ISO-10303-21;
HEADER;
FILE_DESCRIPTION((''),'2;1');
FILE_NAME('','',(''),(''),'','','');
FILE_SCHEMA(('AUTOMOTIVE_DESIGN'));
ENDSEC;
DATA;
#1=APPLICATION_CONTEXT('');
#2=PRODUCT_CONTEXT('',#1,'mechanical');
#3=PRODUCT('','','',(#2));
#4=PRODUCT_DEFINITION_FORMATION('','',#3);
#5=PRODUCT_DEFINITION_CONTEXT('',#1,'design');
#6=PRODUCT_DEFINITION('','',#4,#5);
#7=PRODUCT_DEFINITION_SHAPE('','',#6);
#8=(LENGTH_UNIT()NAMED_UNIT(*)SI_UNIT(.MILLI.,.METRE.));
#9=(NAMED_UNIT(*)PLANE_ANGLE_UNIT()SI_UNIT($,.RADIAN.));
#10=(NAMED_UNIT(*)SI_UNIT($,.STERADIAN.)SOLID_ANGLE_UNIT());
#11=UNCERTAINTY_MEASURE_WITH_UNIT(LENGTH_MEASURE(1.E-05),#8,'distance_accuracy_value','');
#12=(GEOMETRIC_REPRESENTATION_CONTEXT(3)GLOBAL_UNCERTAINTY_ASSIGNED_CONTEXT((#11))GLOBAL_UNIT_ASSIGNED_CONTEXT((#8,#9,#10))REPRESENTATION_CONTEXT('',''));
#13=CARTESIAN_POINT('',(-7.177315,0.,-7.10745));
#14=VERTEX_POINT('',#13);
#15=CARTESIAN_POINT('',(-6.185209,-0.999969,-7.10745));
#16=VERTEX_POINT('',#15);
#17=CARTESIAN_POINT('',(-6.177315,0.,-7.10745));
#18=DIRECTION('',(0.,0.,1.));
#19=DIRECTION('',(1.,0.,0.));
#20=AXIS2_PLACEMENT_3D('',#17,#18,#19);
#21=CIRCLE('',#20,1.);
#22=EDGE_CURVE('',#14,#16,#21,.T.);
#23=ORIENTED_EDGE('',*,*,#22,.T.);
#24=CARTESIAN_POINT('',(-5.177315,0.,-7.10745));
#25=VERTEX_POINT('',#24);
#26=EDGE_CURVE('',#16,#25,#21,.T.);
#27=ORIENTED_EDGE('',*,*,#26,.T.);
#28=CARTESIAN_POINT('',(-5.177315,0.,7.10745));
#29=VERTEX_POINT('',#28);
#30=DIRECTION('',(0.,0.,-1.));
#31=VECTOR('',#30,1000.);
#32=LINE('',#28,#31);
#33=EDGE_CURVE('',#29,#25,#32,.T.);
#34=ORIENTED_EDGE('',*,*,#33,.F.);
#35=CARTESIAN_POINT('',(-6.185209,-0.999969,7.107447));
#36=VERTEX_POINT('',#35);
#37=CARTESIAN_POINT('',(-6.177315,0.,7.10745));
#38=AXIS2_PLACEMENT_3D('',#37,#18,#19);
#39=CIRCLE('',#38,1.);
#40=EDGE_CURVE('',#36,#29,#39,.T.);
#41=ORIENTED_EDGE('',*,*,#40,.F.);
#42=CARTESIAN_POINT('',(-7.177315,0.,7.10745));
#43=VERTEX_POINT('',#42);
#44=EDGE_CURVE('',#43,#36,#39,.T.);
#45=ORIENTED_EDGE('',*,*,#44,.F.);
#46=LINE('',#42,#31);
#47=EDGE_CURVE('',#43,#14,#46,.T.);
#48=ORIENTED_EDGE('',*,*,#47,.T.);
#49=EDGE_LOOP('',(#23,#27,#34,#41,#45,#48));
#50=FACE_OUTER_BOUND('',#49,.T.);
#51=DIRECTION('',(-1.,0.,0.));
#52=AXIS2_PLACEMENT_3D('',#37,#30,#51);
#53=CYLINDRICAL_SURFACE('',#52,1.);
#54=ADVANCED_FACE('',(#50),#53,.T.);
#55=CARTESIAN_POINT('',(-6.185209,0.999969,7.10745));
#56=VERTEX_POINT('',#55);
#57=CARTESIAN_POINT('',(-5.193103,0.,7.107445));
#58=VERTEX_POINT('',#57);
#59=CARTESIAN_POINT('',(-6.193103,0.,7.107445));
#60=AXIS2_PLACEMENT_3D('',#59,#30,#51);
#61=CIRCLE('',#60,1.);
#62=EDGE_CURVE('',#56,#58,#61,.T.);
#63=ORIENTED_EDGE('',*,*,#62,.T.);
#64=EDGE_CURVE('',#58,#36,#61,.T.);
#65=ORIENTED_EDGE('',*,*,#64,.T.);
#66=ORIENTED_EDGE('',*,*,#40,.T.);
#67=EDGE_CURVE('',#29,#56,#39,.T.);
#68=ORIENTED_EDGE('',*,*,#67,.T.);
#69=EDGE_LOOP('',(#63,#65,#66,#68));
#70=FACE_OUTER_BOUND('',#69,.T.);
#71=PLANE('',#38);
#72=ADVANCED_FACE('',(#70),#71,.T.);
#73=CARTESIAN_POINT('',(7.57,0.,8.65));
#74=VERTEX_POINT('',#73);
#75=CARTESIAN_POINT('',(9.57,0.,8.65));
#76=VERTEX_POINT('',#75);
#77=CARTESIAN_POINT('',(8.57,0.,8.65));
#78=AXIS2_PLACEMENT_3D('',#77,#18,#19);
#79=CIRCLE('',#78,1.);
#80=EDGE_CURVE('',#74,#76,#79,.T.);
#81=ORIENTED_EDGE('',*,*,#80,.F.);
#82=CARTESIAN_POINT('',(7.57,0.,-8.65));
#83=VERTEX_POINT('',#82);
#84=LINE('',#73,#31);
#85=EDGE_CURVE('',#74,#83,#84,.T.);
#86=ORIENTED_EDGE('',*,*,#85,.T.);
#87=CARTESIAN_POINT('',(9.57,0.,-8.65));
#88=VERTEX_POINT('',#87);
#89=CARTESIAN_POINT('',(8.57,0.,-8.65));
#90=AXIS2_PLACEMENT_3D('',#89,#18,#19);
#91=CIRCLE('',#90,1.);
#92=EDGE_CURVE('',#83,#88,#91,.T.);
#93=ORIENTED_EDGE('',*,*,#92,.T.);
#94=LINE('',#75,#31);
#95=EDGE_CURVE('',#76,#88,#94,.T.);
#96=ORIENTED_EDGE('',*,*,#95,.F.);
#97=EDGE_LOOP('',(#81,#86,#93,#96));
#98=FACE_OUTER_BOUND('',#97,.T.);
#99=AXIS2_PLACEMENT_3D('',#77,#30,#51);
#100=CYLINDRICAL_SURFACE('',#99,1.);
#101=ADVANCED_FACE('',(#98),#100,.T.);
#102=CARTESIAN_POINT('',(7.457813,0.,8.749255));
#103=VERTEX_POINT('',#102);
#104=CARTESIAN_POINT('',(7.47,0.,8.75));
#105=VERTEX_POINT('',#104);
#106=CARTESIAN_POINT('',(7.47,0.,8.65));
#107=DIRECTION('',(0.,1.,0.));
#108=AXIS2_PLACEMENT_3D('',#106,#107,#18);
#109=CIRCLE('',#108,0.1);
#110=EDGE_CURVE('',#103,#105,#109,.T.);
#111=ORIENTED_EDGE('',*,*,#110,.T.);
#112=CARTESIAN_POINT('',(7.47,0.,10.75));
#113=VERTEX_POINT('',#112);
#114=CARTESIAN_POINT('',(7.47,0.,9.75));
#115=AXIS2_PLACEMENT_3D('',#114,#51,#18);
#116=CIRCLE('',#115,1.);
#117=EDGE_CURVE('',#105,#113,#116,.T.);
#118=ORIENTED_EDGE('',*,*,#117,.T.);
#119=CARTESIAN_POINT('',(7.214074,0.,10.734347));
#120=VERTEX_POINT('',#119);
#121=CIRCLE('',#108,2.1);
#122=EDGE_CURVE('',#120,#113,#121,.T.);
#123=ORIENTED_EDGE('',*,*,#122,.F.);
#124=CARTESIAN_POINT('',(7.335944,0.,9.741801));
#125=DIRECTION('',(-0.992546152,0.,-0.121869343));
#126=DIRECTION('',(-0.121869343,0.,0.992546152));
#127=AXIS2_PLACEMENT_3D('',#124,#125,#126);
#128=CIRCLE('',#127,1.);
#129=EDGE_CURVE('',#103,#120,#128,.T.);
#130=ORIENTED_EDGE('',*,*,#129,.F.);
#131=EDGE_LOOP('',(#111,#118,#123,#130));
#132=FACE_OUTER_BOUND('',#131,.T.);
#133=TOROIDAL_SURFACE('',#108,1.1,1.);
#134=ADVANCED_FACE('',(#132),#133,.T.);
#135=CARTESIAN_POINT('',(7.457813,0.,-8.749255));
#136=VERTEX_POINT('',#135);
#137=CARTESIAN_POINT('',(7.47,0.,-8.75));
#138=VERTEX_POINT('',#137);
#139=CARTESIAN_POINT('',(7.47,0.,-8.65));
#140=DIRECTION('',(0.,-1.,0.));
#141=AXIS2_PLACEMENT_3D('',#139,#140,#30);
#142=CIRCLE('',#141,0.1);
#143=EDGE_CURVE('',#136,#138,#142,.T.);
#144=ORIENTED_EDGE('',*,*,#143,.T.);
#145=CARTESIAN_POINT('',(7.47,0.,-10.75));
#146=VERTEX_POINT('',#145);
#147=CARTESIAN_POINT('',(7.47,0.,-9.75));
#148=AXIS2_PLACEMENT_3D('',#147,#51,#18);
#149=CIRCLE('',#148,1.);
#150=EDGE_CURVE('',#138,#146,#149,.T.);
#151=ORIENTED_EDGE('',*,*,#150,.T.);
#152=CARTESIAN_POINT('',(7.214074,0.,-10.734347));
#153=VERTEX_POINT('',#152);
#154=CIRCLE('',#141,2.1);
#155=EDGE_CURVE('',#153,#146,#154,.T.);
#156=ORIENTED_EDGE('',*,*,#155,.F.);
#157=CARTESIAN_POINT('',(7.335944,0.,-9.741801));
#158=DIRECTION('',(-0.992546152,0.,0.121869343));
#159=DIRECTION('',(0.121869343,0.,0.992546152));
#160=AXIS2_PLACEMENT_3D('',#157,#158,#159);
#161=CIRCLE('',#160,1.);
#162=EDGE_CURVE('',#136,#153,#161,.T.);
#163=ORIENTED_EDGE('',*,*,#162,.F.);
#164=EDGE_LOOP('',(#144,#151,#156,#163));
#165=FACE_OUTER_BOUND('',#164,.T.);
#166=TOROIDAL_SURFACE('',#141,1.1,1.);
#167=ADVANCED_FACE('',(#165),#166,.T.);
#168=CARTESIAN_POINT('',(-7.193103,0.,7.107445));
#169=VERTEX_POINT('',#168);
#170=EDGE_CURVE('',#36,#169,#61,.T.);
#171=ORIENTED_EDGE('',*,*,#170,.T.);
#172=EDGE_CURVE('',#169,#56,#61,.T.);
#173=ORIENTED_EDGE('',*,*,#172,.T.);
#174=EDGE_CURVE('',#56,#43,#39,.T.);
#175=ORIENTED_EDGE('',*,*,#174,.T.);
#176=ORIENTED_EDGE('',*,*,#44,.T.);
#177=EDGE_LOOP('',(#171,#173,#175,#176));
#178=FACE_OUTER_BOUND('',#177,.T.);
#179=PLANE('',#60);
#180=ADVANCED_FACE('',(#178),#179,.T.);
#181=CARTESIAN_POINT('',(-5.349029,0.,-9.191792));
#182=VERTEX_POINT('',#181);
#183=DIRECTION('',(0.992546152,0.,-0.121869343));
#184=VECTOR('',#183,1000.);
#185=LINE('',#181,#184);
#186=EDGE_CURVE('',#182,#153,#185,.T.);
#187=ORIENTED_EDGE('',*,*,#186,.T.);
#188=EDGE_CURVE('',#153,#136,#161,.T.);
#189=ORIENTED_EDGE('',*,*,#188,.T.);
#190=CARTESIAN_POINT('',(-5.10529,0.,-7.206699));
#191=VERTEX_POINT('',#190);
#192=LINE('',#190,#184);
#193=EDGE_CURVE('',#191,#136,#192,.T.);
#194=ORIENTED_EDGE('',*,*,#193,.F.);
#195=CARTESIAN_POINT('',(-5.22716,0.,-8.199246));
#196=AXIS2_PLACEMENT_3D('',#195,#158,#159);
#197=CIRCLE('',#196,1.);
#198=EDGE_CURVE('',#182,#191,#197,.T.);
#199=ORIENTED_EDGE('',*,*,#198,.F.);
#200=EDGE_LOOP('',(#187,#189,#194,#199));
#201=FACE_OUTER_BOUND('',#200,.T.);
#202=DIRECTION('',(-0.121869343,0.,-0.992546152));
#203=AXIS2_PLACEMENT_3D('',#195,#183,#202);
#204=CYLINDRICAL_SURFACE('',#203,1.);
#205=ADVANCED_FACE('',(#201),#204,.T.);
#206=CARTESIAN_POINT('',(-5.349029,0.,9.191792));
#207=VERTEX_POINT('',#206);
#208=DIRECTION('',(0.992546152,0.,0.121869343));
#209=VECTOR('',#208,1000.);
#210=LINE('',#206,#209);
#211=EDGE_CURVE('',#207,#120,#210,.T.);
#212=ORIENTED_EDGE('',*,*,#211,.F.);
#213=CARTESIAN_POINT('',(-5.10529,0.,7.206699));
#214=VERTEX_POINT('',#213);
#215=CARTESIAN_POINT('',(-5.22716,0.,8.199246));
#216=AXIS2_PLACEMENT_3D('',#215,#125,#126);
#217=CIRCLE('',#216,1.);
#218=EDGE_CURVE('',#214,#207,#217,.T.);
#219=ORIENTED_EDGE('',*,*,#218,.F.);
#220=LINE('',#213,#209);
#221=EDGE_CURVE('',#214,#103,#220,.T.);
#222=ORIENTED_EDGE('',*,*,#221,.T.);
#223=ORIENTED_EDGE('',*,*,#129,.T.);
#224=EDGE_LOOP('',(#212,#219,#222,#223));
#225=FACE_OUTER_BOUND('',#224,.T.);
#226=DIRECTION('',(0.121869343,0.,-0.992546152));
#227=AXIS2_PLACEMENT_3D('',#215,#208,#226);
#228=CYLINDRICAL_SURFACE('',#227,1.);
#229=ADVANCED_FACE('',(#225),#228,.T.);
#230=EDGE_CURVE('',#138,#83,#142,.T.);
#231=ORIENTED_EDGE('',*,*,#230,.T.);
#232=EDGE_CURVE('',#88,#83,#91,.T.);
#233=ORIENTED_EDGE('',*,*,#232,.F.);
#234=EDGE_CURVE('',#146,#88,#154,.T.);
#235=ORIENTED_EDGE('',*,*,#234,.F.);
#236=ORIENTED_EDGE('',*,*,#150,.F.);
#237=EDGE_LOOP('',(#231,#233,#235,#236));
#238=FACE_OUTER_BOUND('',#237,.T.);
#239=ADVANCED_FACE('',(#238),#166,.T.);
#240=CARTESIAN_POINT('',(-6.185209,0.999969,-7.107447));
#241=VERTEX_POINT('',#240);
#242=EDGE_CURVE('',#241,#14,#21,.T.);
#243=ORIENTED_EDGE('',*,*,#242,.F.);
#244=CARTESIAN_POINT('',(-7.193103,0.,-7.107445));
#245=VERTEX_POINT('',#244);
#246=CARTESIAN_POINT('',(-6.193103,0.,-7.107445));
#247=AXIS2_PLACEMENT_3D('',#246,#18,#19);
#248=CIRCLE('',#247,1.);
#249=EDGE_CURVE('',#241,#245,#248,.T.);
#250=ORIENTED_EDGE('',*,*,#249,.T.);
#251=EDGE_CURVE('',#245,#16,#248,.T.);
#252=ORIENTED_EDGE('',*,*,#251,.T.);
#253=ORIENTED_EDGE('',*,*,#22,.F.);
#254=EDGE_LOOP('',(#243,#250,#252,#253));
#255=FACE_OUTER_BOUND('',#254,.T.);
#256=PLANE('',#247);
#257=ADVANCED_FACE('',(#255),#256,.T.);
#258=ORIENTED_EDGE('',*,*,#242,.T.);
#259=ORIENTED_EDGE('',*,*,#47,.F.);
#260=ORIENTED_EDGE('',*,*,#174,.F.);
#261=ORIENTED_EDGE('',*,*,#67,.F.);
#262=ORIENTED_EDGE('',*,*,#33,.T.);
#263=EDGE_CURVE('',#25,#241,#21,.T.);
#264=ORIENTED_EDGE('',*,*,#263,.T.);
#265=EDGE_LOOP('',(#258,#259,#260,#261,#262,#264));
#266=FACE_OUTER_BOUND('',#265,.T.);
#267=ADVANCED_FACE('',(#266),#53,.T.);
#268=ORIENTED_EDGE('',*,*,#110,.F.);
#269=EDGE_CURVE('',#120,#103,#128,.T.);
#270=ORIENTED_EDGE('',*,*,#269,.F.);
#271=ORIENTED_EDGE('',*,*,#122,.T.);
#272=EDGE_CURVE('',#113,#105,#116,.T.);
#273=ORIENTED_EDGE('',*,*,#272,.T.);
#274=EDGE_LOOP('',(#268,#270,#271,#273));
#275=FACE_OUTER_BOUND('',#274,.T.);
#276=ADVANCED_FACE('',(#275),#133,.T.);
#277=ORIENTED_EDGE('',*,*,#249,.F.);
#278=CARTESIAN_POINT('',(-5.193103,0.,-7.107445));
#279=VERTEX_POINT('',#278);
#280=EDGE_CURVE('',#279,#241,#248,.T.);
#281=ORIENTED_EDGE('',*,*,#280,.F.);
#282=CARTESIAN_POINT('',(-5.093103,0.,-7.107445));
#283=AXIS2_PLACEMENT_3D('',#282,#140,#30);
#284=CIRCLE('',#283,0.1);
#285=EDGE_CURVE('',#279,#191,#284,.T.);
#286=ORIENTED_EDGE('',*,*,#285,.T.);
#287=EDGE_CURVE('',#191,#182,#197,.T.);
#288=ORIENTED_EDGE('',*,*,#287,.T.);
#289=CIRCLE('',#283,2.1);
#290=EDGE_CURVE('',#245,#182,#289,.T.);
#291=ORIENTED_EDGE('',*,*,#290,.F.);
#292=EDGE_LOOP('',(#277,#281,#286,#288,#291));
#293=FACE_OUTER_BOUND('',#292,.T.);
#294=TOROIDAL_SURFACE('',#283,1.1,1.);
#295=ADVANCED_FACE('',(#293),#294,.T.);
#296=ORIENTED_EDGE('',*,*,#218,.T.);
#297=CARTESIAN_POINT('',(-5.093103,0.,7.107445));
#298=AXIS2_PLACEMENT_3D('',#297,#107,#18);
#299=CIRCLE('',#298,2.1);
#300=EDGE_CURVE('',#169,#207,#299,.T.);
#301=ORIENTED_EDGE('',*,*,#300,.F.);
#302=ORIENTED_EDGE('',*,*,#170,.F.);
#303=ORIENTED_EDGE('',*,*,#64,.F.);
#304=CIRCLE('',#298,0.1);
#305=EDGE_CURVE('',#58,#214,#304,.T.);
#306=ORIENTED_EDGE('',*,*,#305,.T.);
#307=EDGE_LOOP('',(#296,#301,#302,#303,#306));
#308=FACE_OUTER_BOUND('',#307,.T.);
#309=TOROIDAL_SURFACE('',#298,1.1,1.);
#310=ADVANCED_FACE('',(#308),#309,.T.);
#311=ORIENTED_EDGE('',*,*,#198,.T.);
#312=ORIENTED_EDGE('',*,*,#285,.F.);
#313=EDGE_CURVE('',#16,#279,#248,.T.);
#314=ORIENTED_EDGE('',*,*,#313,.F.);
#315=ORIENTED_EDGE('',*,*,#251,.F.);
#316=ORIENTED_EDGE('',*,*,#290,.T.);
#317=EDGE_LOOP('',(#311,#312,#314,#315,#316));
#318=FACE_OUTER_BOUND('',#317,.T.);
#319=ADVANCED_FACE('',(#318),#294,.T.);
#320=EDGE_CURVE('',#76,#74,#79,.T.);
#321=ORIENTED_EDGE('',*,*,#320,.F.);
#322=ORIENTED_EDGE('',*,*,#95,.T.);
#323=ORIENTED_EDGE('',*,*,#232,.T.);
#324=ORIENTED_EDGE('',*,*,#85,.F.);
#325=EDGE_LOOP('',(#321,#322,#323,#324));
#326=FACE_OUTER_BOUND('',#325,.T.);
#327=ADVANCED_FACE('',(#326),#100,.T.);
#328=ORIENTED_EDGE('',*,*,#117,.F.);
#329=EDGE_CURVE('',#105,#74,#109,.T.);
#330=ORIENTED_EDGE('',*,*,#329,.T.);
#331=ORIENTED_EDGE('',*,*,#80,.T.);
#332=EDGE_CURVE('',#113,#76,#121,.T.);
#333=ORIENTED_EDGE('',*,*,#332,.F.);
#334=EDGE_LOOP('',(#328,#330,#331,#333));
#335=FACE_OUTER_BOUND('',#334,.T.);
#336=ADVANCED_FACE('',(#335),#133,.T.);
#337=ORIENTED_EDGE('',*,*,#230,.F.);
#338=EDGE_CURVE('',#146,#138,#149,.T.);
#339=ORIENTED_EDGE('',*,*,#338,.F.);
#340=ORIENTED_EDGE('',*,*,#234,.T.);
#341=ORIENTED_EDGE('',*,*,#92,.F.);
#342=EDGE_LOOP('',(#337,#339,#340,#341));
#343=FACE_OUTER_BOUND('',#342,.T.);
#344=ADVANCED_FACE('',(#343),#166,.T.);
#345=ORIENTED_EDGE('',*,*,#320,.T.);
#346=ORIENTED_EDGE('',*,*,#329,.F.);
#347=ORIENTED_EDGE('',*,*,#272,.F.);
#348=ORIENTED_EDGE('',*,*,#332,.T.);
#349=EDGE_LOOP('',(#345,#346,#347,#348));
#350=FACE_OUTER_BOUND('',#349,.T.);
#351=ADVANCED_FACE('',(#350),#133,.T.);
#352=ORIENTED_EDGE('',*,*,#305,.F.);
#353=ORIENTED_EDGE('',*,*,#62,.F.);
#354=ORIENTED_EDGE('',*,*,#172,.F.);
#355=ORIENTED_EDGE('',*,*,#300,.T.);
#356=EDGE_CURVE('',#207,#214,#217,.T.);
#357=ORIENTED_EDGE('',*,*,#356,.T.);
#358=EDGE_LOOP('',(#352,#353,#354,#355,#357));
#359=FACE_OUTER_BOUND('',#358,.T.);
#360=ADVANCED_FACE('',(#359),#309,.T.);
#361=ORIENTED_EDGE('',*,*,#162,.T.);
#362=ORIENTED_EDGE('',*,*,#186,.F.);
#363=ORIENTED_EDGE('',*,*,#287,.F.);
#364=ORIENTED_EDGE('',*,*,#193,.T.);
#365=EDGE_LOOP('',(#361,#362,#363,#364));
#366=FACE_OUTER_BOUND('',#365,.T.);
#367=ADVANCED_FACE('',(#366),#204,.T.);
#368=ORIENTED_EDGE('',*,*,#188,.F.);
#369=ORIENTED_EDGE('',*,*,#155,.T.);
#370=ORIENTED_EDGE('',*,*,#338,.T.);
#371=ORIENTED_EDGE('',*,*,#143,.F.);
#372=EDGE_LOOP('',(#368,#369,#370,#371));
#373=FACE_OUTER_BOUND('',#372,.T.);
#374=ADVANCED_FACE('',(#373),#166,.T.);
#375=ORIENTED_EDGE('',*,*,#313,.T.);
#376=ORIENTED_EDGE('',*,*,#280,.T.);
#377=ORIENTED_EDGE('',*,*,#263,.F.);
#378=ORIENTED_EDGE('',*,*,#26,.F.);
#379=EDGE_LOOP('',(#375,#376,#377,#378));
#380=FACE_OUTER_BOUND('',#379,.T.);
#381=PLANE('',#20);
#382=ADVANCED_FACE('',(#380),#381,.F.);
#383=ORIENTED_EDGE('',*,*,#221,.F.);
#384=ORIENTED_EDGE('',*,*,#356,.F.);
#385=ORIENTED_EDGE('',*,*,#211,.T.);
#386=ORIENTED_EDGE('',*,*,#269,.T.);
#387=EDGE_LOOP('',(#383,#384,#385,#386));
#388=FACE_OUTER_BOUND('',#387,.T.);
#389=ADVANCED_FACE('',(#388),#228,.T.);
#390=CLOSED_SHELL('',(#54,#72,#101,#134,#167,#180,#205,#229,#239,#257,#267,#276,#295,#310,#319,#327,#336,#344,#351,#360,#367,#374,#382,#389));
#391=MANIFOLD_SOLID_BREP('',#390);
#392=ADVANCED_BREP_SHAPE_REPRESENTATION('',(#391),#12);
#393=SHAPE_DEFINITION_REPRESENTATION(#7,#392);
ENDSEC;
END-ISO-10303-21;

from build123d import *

# Parameters (mm, degrees)
EXTRUDE_1_DEPTH      = 8.65
EXTRUDE_1_DEPTH_BACK = 8.65
SKETCH_1_R           = 1
SKETCH_2_R           = 1
REVOLVE_1_ANGLE      = 97
SKETCH_3_R           = 1
REVOLVE_2_ANGLE      = 97
SKETCH_4_R           = 1
EXTRUDE_2_DEPTH      = 12.65745
SKETCH_5_R           = 1
EXTRUDE_3_DEPTH      = 12.65745
SKETCH_6_R           = 1
REVOLVE_3_ANGLE      = 83
SKETCH_7_R           = 1
REVOLVE_4_ANGLE      = 83
EXTRUDE_4_DEPTH      = 7.10745
EXTRUDE_4_DEPTH_BACK = 7.10745
SKETCH_8_R           = 1


with BuildPart() as part:
    # 草图1 → 凸台-拉伸1 (new, two sides: drawn at the far end of the back side and taken through both)
    with BuildSketch(Plane.XY.offset(-EXTRUDE_1_DEPTH_BACK)):
        with Locations((8.57, 0)):
            Circle(SKETCH_1_R)
    extrude(amount=EXTRUDE_1_DEPTH + EXTRUDE_1_DEPTH_BACK)

    # 草图2 → 旋转1 (revolve)
    with BuildSketch(Plane(origin=(0, 0, -8.65), x_dir=(-1, 0, 0), z_dir=(0, 0, -1))):
        with Locations(Location((-8.57, 0, 0), (0, 0, 180))):
            Circle(SKETCH_2_R)
    revolve(axis=Axis((7.47, 1, -8.65), (0, 1, 0)), revolution_arc=REVOLVE_1_ANGLE)

    # 草图3 → 旋转2 (revolve)
    with BuildSketch(Plane.XY.offset(8.65)):
        with Locations((8.57, 0)):
            Circle(SKETCH_3_R)
    revolve(axis=Axis((7.47, -1, 8.65), (0, -1, 0)), revolution_arc=REVOLVE_2_ANGLE)

    # 草图4 → 凸台-拉伸2 (add)
    with BuildSketch(Plane(origin=(8.405366736, 0, -1.032049264), x_dir=(0.12186934340514718, 0, 0.9925461516413221), z_dir=(-0.9925461516413221, 0, 0.12186934340514718))):
        with Locations(Location((-8.775160216, 0, 0), (0, 0, 180))):
            Circle(SKETCH_4_R)
    extrude(amount=EXTRUDE_2_DEPTH)

    # 草图5 → 凸台-拉伸3 (add)
    with BuildSketch(Plane(origin=(8.405366736, 0, 1.032049264), x_dir=(-0.12186934340514718, 0, 0.9925461516413221), z_dir=(-0.9925461516413221, 0, -0.12186934340514718))):
        with Locations((8.775160216, 0)):
            Circle(SKETCH_5_R)
    extrude(amount=EXTRUDE_3_DEPTH)

    # 草图6 → 旋转3 (revolve)
    with BuildSketch(Plane(origin=(-4.157736551, 0, 0.510505857), x_dir=(0.12186934340514717, 0, 0.9925461516413221), z_dir=(-0.9925461516413221, 0, 0.12186934340514717))):
        with Locations(Location((-8.775160216, 0, 0), (0, 0, 180))):
            Circle(SKETCH_6_R)
    revolve(axis=Axis((-5.093103287, 1, -7.107444879), (0, 1, 0)), revolution_arc=REVOLVE_3_ANGLE)

    # 草图7 → 旋转4 (revolve)
    with BuildSketch(Plane(origin=(-4.157736551, 0, -0.510505857), x_dir=(-0.12186934340514716, 0, 0.9925461516413221), z_dir=(-0.9925461516413221, 0, -0.12186934340514716))):
        with Locations((8.775160216, 0)):
            Circle(SKETCH_7_R)
    revolve(axis=Axis((-5.093103287, -1, 7.107444879), (0, -1, 0)), revolution_arc=REVOLVE_4_ANGLE)

    # 草图8 → 凸台-拉伸4 (add, two sides: drawn at the far end of the back side and taken through both)
    with BuildSketch(Plane.XY.offset(-EXTRUDE_4_DEPTH_BACK)):
        with Locations(Location((-6.177315, 0, 0), (0, 0, 90.452305782))):
            Circle(SKETCH_8_R)
    extrude(amount=EXTRUDE_4_DEPTH + EXTRUDE_4_DEPTH_BACK)


solid = part.part
